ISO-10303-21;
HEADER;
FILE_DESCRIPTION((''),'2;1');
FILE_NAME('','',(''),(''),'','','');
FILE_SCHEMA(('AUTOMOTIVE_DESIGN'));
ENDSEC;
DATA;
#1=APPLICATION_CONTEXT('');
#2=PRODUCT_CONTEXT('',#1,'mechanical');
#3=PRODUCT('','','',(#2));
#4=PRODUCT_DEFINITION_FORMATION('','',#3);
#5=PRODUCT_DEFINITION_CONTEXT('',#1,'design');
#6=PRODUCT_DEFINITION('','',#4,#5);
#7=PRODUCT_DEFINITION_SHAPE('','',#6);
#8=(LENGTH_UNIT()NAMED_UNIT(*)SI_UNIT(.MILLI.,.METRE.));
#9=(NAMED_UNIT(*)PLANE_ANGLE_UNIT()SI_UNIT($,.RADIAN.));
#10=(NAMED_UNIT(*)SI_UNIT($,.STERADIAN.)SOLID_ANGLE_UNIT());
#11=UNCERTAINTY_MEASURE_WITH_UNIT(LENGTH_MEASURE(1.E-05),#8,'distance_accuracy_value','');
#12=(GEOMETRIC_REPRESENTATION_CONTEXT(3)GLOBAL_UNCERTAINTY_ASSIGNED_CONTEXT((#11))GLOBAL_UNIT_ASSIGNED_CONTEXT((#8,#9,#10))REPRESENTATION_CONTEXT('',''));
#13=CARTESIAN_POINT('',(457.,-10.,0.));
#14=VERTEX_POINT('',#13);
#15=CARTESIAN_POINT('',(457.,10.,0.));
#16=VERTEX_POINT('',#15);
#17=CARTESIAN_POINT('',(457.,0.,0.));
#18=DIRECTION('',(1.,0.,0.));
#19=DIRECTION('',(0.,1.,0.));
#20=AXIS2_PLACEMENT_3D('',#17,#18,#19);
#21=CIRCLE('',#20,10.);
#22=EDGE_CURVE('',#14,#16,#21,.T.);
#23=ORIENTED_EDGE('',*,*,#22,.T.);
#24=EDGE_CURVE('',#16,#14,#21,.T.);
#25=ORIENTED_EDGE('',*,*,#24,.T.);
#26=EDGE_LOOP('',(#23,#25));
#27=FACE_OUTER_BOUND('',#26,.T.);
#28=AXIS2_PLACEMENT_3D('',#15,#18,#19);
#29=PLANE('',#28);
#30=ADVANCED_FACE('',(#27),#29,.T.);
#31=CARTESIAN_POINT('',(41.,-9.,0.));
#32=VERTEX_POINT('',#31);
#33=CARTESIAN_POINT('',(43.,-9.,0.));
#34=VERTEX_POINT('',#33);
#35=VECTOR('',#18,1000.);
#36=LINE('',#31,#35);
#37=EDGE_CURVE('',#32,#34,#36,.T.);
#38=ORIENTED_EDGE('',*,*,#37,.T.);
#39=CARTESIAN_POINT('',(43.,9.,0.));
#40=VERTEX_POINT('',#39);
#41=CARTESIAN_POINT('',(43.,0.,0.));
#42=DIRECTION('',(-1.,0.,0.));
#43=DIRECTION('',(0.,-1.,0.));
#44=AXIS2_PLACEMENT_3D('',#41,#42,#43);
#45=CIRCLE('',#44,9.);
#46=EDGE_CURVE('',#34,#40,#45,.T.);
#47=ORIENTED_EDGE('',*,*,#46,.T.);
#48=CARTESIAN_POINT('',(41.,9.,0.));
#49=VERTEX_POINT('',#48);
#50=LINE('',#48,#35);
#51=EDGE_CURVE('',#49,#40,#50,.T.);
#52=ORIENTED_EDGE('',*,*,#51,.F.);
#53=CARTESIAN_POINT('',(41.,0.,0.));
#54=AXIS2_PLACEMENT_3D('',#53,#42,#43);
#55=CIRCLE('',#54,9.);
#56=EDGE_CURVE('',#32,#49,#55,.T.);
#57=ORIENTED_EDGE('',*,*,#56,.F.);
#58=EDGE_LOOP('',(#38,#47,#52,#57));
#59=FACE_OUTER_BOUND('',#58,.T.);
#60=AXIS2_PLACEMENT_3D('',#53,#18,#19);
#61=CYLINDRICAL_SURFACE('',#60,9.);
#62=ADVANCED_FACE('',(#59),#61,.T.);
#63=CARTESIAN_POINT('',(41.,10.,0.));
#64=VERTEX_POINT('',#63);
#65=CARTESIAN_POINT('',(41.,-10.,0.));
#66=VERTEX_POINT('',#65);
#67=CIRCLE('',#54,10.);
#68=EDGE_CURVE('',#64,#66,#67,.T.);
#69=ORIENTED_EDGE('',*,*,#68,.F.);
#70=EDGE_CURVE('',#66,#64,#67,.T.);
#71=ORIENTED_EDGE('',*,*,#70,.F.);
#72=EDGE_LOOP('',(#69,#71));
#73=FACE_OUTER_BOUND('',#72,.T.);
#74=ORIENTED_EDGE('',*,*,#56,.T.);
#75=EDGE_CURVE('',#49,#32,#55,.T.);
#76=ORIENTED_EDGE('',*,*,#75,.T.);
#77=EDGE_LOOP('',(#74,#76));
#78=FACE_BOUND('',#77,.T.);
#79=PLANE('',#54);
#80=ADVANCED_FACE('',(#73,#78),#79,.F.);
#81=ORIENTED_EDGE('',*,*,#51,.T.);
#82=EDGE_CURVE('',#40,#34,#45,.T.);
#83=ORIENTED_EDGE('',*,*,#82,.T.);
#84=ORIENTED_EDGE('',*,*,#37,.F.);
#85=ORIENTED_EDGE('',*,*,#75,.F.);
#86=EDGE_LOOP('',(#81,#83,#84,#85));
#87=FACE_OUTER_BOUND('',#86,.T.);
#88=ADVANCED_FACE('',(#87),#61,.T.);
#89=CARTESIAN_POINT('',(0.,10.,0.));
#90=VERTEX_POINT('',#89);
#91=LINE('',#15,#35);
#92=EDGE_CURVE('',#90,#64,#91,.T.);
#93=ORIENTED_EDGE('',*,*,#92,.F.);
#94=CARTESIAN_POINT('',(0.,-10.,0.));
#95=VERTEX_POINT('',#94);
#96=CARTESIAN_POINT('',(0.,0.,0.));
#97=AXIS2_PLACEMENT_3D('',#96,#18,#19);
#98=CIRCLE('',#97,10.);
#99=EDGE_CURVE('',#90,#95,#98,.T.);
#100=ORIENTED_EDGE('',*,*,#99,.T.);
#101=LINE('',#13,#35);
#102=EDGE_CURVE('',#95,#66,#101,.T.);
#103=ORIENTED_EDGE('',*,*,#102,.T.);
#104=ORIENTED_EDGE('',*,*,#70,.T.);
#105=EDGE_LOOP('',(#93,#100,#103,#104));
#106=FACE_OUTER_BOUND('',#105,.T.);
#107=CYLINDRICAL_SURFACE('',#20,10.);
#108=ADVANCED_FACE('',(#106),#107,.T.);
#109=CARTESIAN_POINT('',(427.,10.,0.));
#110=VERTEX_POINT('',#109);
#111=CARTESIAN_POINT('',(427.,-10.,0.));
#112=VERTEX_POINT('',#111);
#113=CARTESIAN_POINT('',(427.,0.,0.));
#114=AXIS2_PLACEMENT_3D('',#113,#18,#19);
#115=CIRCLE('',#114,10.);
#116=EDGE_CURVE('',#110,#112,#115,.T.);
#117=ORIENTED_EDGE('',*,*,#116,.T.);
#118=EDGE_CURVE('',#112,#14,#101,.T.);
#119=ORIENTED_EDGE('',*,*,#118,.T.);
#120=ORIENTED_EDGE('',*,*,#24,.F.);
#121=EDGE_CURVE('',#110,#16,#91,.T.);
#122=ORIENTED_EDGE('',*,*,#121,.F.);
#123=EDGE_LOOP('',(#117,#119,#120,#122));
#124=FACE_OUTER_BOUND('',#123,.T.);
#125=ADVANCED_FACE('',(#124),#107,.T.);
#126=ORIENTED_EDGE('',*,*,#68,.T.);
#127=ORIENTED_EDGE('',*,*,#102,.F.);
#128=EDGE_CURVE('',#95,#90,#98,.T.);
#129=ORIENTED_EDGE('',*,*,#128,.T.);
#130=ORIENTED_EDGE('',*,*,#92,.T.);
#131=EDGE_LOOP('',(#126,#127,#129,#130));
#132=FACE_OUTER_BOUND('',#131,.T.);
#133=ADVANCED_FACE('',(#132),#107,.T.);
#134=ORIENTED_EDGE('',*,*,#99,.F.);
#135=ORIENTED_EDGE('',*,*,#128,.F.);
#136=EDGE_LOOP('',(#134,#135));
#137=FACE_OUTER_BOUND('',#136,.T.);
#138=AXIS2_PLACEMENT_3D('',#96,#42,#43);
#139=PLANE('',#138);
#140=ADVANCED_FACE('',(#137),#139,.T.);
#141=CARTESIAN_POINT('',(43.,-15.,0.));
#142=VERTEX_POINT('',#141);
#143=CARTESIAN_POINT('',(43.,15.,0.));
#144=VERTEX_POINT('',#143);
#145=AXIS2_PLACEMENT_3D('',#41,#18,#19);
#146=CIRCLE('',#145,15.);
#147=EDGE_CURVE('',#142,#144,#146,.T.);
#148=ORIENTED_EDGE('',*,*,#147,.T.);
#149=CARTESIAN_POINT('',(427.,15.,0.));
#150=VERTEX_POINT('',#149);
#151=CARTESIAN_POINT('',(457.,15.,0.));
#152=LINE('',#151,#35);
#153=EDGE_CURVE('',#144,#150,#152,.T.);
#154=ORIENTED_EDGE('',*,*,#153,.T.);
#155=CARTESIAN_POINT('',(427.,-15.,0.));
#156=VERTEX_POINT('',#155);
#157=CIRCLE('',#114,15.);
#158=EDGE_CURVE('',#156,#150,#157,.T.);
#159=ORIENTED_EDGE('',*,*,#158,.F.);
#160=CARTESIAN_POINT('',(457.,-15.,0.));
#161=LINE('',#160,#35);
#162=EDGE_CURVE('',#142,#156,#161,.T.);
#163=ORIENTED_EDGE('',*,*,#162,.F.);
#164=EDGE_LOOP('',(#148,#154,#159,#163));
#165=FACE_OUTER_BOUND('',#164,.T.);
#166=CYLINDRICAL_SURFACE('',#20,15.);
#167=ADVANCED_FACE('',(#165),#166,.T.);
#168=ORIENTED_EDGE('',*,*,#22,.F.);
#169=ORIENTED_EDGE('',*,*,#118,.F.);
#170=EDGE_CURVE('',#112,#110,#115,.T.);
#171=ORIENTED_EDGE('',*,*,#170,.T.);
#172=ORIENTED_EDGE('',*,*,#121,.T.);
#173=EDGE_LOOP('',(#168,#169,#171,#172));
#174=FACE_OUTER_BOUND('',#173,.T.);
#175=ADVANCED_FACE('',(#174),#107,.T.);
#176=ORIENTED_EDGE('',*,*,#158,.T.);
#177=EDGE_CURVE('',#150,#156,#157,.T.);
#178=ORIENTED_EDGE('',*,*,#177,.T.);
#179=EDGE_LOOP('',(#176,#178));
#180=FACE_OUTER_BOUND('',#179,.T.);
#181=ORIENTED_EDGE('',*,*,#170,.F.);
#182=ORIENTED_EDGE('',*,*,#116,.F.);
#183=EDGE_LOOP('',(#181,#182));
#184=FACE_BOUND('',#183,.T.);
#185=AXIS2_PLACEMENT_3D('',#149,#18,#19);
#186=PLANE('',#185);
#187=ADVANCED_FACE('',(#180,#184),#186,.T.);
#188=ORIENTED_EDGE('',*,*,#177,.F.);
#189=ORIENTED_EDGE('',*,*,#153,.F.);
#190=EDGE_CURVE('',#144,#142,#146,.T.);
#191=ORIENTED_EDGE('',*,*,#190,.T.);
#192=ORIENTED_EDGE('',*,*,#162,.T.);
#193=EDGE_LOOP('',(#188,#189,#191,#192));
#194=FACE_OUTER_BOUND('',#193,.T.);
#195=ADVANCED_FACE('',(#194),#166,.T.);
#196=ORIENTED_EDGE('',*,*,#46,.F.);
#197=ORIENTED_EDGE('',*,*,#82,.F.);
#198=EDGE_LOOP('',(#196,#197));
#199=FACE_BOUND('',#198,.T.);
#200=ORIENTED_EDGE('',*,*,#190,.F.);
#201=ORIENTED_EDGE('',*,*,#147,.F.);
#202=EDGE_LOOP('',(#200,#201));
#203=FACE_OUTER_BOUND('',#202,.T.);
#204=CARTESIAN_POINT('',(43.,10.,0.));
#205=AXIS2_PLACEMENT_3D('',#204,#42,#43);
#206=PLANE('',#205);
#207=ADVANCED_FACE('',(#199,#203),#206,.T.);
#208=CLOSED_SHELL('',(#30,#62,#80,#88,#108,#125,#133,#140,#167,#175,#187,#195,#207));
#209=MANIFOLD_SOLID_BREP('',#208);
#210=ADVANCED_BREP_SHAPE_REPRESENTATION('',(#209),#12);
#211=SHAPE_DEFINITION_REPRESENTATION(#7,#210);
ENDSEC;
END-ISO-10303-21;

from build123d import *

# Parameters (mm, degrees)
SKETCH_2_R          = 10
SKETCH_2_R_2        = 9
CUT_EXTRUDE_1_DEPTH = 2


with BuildPart() as part:
    # 草图1 → 旋转1 (revolve)
    with BuildSketch(Plane.XY):
        Polygon((0, 0), (0, 10), (43, 10), (43, 15), (427, 15), (427, 10), (457, 10), (457, 0), align=None)
    revolve(axis=Axis((457, 0, 0), (-1, 0, 0)))

    # 草图2 → 切除-拉伸1 (cut)
    with BuildSketch(Plane.ZY.offset(-43)):
        with Locations(Location((0, 0, 0), (0, 0, 90))):
            Circle(SKETCH_2_R)
        with Locations(Location((0, 0, 0), (0, 0, 270))):
            Circle(SKETCH_2_R_2, mode=Mode.SUBTRACT)
    extrude(amount=CUT_EXTRUDE_1_DEPTH, mode=Mode.SUBTRACT)


solid = part.part
